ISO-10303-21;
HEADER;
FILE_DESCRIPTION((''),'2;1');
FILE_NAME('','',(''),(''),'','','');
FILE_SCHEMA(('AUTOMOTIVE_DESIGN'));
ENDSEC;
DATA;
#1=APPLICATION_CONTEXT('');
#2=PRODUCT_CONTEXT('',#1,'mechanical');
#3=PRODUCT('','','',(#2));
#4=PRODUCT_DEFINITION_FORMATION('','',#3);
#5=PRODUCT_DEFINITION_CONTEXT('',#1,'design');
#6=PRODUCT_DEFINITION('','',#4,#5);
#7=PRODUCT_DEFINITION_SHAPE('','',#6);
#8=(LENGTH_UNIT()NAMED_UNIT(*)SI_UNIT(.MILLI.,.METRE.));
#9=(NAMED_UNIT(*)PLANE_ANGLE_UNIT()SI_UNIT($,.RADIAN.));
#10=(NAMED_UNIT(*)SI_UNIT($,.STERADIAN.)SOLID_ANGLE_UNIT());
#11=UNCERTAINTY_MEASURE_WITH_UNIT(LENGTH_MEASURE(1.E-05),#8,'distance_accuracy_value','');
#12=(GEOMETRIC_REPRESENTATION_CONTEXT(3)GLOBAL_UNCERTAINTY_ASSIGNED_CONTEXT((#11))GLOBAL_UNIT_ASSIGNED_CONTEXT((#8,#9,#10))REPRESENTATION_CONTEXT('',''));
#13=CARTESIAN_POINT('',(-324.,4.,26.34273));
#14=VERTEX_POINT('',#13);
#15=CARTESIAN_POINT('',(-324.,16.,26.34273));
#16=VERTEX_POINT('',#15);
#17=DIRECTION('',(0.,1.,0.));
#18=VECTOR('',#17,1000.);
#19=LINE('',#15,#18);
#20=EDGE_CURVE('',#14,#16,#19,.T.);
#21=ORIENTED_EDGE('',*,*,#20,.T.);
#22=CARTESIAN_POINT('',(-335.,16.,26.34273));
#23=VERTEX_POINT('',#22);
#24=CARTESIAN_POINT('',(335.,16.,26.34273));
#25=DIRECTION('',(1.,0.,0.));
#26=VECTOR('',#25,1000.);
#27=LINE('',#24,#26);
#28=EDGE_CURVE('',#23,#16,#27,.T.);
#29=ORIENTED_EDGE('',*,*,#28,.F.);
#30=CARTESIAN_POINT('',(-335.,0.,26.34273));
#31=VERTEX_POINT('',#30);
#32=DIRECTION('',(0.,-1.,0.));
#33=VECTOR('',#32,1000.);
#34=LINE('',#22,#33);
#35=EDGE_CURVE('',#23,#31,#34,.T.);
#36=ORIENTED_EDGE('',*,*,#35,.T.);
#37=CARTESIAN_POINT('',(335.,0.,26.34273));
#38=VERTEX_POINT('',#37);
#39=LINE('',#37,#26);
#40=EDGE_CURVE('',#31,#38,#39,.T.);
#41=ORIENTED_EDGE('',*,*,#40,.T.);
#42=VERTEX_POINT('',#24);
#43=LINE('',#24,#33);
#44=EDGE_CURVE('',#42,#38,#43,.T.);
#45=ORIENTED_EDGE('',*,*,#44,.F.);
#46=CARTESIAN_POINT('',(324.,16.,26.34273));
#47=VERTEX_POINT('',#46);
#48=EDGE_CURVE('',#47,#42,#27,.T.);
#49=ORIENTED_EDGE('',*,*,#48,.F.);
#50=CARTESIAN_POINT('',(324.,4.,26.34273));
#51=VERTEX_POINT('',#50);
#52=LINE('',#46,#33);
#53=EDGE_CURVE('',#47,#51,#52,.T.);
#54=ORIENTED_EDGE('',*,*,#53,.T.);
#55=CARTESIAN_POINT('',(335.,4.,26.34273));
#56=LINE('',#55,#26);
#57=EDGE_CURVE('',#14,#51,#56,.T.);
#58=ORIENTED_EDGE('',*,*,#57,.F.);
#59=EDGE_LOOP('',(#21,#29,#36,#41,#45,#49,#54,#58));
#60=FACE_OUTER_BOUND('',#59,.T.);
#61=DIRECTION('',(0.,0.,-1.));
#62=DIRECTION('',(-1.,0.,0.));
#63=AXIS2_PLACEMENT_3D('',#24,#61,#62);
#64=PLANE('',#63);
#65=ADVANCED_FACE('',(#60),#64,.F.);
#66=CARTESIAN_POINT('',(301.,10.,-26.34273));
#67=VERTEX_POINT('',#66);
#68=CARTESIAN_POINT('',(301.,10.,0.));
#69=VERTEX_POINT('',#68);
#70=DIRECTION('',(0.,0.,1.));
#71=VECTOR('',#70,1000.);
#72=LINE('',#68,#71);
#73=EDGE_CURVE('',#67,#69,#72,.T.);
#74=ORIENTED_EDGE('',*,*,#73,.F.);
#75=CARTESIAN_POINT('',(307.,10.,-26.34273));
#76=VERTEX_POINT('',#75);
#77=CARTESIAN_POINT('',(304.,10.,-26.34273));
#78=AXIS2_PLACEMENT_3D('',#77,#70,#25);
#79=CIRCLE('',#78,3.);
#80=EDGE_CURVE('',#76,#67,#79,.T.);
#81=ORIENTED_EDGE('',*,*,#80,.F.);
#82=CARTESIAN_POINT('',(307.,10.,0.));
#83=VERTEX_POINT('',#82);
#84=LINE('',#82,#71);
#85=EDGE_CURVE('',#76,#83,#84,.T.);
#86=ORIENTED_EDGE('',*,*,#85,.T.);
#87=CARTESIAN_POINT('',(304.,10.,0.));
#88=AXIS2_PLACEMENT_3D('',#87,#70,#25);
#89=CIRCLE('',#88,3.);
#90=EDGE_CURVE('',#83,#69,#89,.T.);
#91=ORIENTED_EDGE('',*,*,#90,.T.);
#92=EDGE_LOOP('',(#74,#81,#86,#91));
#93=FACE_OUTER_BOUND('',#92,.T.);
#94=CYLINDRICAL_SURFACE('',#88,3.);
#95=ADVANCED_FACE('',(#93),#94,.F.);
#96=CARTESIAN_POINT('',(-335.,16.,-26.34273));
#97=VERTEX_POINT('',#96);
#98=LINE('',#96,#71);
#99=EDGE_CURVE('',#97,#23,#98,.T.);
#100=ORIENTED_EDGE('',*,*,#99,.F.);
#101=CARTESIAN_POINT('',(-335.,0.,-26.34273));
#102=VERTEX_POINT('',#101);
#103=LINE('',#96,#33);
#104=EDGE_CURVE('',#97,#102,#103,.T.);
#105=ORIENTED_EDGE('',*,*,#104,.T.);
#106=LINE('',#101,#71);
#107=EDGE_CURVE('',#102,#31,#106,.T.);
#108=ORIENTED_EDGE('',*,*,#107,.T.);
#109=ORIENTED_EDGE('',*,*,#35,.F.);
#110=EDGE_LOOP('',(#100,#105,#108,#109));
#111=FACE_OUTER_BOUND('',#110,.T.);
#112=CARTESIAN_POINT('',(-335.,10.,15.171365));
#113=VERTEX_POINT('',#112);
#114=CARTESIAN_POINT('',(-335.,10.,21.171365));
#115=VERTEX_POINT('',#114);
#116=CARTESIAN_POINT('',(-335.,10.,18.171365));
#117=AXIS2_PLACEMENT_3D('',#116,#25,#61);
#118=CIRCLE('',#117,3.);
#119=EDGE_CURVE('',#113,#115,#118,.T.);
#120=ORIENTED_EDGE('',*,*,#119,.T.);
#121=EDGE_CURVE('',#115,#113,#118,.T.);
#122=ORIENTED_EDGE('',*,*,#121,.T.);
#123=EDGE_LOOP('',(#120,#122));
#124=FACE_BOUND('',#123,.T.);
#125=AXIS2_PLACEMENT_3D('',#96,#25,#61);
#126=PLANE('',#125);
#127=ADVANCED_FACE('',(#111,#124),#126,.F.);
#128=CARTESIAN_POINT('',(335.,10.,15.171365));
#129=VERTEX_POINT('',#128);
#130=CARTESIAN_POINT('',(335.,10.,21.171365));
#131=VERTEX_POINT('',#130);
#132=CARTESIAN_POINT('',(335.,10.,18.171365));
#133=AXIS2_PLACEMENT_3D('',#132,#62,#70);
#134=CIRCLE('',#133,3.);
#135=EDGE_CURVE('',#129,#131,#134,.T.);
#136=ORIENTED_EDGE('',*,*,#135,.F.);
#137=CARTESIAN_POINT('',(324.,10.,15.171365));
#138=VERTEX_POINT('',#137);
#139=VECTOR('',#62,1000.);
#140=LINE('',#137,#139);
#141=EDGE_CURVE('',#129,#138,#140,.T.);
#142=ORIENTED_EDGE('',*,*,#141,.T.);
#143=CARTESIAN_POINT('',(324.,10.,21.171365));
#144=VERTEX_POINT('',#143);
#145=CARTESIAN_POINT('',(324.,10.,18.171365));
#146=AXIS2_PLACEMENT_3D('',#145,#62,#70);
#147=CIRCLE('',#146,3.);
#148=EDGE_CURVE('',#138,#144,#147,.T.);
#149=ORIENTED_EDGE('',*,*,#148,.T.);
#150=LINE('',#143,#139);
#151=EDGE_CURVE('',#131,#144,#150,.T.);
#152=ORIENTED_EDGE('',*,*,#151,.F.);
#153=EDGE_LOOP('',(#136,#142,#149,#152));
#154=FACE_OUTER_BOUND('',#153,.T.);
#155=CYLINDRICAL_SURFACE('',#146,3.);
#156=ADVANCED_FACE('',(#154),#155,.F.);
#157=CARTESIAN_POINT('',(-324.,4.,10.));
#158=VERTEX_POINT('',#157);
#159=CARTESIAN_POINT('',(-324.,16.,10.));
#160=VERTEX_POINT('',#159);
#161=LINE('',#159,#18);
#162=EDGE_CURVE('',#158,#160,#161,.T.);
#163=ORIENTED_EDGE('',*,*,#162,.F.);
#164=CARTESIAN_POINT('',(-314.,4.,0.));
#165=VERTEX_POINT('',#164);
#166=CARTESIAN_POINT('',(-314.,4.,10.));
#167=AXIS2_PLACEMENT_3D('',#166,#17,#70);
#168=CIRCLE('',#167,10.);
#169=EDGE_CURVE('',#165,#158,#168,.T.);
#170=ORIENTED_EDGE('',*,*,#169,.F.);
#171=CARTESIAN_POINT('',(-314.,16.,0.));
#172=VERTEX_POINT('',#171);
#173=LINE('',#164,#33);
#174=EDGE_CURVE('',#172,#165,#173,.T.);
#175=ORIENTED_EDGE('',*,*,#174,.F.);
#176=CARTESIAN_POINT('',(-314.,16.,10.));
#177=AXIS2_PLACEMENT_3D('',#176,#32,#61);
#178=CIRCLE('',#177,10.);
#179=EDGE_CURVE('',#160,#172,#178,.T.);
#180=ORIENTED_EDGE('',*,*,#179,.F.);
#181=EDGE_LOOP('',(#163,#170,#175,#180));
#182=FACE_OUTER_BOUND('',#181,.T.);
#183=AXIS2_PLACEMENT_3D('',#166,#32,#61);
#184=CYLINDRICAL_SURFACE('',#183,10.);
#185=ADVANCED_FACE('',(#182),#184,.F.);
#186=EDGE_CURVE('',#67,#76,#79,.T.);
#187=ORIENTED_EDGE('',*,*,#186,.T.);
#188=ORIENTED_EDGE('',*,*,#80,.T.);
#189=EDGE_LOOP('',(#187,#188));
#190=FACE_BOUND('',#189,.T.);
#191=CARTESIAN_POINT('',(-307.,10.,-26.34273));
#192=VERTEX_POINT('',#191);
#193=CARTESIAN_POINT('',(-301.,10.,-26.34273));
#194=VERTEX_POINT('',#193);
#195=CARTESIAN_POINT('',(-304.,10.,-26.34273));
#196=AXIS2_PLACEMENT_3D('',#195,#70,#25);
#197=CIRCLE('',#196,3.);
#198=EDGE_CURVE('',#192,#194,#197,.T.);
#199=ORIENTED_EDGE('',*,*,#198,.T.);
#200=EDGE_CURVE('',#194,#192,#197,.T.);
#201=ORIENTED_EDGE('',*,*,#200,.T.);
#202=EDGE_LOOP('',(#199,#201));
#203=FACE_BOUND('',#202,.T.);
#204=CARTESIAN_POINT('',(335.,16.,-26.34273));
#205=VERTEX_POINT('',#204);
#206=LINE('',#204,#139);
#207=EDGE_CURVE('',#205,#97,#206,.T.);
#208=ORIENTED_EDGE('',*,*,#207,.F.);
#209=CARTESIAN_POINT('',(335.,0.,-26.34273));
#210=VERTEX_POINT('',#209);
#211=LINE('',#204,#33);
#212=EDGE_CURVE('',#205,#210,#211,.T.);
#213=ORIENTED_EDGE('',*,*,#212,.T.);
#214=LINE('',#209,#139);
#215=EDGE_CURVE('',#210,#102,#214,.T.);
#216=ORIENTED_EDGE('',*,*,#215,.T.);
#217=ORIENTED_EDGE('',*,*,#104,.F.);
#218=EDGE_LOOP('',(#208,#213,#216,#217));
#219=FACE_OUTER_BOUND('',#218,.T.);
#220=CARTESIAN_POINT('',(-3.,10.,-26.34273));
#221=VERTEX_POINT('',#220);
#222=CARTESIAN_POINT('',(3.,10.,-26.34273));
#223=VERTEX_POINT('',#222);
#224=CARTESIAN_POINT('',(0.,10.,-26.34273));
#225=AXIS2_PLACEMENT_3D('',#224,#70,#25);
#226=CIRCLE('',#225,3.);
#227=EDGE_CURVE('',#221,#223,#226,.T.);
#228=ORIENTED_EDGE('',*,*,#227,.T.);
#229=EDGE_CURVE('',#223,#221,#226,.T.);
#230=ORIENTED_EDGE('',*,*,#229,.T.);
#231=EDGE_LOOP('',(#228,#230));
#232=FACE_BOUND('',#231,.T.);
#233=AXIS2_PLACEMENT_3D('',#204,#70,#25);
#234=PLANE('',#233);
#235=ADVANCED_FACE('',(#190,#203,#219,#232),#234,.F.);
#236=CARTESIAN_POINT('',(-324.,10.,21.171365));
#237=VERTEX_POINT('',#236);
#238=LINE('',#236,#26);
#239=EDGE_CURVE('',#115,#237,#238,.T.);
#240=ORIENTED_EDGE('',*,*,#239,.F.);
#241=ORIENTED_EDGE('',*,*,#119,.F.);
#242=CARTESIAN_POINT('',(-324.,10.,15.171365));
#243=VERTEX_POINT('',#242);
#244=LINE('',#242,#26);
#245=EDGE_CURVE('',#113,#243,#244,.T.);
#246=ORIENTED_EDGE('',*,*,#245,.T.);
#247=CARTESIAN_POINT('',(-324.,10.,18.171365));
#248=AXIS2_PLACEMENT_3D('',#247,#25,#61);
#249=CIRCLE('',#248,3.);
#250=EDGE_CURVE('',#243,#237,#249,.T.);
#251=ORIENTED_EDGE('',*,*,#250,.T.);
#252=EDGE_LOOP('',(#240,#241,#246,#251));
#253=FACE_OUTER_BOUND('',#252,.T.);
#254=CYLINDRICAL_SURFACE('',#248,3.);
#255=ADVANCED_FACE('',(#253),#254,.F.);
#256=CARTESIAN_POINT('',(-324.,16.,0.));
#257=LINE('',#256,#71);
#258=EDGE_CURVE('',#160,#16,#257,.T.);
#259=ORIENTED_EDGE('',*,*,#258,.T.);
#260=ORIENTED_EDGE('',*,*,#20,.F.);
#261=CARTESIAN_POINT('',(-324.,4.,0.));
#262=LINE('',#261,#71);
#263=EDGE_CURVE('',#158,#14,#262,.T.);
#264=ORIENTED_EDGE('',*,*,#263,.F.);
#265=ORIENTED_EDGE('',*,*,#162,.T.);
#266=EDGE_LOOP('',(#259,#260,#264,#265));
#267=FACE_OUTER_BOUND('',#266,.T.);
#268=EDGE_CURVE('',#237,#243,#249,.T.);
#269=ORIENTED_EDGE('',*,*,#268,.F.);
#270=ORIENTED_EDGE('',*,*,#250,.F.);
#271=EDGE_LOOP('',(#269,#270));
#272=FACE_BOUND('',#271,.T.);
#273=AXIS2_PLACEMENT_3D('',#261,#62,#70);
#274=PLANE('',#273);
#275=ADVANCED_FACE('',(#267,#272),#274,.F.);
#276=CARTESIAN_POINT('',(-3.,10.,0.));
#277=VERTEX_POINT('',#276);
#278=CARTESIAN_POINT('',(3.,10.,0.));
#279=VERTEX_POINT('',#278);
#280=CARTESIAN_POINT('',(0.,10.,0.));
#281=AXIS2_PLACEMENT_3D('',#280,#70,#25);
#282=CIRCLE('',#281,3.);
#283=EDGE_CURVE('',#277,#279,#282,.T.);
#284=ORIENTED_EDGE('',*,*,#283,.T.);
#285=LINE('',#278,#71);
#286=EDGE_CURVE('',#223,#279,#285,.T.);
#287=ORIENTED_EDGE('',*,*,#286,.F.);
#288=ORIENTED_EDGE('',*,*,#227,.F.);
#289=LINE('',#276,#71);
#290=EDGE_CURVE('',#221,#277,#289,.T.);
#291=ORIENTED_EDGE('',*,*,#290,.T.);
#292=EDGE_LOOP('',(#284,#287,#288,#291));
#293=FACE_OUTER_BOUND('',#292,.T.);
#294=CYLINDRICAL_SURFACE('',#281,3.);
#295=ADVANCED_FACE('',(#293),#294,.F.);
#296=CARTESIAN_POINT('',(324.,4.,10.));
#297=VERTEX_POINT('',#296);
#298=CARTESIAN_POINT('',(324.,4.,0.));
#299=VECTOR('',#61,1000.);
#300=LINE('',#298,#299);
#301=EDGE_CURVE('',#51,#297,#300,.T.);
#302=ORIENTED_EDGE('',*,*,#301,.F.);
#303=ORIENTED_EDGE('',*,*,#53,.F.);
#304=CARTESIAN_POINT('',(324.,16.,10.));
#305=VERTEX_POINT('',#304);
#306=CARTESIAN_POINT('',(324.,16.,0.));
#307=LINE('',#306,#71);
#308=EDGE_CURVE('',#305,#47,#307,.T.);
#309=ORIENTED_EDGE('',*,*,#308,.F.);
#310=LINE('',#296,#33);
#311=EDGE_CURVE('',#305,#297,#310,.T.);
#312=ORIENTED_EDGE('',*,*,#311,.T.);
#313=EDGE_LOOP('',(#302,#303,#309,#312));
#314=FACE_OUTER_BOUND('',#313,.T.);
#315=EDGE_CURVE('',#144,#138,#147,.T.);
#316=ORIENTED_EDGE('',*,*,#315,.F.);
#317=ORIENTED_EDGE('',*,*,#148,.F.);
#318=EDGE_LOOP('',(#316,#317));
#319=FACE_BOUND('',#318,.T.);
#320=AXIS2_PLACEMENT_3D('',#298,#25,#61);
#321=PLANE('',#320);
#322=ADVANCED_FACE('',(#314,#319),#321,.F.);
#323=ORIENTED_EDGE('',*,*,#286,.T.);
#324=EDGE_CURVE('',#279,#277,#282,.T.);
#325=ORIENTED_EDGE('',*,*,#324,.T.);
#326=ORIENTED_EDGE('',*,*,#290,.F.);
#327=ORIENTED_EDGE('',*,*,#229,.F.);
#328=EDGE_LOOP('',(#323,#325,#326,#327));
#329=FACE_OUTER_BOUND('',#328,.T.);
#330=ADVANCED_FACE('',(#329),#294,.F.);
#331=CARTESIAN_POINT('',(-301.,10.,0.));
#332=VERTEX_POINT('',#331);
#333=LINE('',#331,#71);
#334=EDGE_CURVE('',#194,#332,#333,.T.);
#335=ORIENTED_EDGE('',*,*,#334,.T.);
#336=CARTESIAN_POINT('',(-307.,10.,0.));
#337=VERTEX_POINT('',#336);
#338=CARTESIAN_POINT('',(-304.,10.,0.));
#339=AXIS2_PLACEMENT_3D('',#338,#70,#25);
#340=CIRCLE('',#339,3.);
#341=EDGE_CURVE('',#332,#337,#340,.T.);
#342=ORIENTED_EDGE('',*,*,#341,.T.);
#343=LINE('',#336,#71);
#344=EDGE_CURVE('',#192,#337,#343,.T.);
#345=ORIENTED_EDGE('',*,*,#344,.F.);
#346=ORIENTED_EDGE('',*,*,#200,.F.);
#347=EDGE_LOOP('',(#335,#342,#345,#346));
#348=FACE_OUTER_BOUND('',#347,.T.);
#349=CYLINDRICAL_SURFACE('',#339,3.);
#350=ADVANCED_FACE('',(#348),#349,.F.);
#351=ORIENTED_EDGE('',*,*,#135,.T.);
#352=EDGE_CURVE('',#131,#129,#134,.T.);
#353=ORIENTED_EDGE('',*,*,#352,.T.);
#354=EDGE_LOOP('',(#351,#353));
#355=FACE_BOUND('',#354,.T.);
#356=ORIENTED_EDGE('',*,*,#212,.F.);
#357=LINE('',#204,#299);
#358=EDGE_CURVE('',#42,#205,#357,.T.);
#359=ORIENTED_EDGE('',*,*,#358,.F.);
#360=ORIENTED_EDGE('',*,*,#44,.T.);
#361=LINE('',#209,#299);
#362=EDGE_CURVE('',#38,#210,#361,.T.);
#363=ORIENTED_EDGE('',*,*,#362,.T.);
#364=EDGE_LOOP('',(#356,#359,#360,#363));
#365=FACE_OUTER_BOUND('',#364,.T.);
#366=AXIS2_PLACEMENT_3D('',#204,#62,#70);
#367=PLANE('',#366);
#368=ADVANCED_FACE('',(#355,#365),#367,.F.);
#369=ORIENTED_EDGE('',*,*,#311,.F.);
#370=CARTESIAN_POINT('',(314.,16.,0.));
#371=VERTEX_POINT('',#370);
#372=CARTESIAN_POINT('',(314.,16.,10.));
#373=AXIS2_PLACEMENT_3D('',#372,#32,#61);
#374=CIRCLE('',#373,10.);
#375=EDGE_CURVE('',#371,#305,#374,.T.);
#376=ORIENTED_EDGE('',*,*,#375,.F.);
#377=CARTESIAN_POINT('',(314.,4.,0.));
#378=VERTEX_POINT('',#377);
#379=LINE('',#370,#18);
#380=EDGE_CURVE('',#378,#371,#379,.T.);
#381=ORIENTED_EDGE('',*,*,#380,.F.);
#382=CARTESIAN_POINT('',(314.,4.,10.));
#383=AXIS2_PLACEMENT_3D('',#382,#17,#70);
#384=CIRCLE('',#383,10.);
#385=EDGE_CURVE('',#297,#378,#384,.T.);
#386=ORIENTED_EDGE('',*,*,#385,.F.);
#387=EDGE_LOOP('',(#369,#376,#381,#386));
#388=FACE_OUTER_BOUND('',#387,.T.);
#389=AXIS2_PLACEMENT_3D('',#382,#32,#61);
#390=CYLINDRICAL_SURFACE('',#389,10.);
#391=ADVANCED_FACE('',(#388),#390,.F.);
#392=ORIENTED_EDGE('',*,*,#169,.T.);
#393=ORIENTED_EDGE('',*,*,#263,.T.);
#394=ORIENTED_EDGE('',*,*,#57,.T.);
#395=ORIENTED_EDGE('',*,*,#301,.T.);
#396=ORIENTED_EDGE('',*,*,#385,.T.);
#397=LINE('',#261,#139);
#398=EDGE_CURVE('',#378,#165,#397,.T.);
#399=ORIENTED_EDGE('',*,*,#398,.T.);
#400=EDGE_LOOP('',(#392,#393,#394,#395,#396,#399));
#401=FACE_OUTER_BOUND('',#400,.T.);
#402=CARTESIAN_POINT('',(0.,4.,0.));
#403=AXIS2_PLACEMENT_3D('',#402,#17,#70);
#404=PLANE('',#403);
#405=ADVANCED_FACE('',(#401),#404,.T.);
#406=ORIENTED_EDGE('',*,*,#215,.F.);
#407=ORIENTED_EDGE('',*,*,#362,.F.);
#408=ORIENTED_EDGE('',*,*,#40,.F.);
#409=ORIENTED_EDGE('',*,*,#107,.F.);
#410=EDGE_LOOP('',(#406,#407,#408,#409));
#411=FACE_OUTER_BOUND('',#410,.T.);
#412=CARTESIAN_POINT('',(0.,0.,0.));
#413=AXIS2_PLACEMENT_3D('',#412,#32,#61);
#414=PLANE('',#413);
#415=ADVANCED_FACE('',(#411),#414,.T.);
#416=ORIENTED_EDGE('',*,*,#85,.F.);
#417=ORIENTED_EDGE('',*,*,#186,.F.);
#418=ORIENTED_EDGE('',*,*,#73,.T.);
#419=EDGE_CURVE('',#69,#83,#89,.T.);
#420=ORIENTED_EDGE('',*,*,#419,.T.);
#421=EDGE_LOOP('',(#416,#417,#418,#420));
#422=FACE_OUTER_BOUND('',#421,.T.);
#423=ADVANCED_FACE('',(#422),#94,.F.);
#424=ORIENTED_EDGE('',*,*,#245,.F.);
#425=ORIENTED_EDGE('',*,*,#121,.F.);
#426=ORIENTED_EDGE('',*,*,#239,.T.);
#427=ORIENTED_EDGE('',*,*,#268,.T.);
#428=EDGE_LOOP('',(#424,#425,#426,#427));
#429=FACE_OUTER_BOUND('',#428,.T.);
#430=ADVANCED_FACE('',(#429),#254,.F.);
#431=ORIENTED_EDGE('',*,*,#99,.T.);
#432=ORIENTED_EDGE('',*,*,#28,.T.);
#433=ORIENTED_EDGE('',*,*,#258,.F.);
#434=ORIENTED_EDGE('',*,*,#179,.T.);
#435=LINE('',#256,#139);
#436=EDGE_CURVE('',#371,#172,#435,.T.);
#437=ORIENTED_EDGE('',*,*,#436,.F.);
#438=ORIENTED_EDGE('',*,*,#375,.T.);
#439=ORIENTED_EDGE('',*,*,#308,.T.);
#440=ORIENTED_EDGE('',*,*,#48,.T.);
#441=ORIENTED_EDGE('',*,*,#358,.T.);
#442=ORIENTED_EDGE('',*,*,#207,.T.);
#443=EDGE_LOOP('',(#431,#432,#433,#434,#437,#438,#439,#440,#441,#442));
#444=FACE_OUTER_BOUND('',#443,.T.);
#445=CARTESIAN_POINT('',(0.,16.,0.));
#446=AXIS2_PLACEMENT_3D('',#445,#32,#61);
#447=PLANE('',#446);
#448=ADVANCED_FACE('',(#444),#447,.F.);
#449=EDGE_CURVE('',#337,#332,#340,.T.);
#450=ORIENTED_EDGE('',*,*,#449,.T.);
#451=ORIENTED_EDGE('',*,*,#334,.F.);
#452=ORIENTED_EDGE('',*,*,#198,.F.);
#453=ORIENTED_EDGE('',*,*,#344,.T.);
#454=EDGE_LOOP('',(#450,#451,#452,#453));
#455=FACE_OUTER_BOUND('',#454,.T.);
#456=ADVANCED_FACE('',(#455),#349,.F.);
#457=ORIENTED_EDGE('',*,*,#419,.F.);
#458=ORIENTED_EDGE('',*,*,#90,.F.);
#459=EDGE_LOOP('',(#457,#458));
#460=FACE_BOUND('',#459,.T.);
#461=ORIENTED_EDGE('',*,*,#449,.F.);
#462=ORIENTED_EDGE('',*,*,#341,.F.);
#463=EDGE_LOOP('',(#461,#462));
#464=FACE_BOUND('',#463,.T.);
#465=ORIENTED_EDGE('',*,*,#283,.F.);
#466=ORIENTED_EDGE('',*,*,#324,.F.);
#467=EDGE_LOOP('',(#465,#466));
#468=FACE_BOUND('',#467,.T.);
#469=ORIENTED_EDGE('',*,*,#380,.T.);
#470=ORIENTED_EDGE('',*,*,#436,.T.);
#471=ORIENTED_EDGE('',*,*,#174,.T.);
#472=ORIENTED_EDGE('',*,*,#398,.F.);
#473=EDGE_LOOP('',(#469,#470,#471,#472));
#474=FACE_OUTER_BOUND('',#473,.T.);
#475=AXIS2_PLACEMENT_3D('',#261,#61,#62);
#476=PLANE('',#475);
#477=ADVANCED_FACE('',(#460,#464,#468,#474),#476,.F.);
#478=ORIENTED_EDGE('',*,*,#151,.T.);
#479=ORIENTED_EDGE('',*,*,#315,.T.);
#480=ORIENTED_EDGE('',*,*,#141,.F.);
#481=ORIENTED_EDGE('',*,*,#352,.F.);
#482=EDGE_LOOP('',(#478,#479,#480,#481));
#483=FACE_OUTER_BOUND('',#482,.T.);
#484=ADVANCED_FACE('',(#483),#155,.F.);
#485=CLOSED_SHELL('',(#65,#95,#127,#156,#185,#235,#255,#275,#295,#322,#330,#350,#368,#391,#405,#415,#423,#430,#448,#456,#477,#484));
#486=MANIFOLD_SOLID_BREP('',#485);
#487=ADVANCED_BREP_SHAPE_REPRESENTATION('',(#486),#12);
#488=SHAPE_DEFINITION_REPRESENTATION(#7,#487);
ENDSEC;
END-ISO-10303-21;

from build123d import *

# Parameters (mm, degrees)
SKETCH1_W                 = 670
SKETCH1_H                 = 52.68545994
BOSS_EXTRUDE1_DEPTH       = 16
SKETCH3_W                 = 648
SKETCH3_H                 = 81.022530329
CUT_EXTRUDE2_DEPTH        = 12
FILLET1_R                 = 10
F_6_0MM_DOWEL_HOLE1_D     = 6
F_6_0MM_DOWEL_HOLE1_DEPTH = 11
F_6_0MM_DOWEL_HOLE2_D     = 6


with BuildPart() as part:
    # Sketch1 → Boss-Extrude1 (new body)
    with BuildSketch(Plane(origin=(0, 0, 0), x_dir=(1, 0, 0), z_dir=(0, 1, 0))):
        Rectangle(SKETCH1_W, SKETCH1_H)
    extrude(amount=BOSS_EXTRUDE1_DEPTH)

    # Sketch3 → Cut-Extrude2 (cut)
    with BuildSketch(Plane(origin=(0, 16, 0), x_dir=(1, 0, 0), z_dir=(0, 1, 0))):
        with Locations((0, -40.511265165)):
            Rectangle(SKETCH3_W, SKETCH3_H)
    extrude(amount=-CUT_EXTRUDE2_DEPTH, mode=Mode.SUBTRACT)

    # Fillet1
    fillet1_edges = [part.edges().sort_by_distance(p)[0] for p in [
        (324, 10, 0),
        (-324, 10, 0),
    ]]
    fillet(fillet1_edges, radius=FILLET1_R)

    # Ø6.0mm Dowel Hole1
    with Locations(Plane.ZY.offset(-324)):
        with Locations((18.171364985, 10)):
            f_6_0mm_dowel_hole1 = Hole(F_6_0MM_DOWEL_HOLE1_D / 2, depth=F_6_0MM_DOWEL_HOLE1_DEPTH)

    # Mirror1: Ø6.0mm Dowel Hole1 across plane
    add(f_6_0mm_dowel_hole1.mirror(Plane(origin=(0, 0, 0), x_dir=(0, 0, 1), z_dir=(1, 0, 0))), mode=Mode.SUBTRACT)

    # Ø6.0mm Dowel Hole2 (through all)
    with Locations(Plane.XY):
        with Locations((304, 10), (0, 10)):
            f_6_0mm_dowel_hole2 = Hole(F_6_0MM_DOWEL_HOLE2_D / 2)

    # Mirror2: Ø6.0mm Dowel Hole2 across plane
    add(f_6_0mm_dowel_hole2.mirror(Plane(origin=(0, 0, 0), x_dir=(0, 0, 1), z_dir=(1, 0, 0))), mode=Mode.SUBTRACT)


solid = part.part
